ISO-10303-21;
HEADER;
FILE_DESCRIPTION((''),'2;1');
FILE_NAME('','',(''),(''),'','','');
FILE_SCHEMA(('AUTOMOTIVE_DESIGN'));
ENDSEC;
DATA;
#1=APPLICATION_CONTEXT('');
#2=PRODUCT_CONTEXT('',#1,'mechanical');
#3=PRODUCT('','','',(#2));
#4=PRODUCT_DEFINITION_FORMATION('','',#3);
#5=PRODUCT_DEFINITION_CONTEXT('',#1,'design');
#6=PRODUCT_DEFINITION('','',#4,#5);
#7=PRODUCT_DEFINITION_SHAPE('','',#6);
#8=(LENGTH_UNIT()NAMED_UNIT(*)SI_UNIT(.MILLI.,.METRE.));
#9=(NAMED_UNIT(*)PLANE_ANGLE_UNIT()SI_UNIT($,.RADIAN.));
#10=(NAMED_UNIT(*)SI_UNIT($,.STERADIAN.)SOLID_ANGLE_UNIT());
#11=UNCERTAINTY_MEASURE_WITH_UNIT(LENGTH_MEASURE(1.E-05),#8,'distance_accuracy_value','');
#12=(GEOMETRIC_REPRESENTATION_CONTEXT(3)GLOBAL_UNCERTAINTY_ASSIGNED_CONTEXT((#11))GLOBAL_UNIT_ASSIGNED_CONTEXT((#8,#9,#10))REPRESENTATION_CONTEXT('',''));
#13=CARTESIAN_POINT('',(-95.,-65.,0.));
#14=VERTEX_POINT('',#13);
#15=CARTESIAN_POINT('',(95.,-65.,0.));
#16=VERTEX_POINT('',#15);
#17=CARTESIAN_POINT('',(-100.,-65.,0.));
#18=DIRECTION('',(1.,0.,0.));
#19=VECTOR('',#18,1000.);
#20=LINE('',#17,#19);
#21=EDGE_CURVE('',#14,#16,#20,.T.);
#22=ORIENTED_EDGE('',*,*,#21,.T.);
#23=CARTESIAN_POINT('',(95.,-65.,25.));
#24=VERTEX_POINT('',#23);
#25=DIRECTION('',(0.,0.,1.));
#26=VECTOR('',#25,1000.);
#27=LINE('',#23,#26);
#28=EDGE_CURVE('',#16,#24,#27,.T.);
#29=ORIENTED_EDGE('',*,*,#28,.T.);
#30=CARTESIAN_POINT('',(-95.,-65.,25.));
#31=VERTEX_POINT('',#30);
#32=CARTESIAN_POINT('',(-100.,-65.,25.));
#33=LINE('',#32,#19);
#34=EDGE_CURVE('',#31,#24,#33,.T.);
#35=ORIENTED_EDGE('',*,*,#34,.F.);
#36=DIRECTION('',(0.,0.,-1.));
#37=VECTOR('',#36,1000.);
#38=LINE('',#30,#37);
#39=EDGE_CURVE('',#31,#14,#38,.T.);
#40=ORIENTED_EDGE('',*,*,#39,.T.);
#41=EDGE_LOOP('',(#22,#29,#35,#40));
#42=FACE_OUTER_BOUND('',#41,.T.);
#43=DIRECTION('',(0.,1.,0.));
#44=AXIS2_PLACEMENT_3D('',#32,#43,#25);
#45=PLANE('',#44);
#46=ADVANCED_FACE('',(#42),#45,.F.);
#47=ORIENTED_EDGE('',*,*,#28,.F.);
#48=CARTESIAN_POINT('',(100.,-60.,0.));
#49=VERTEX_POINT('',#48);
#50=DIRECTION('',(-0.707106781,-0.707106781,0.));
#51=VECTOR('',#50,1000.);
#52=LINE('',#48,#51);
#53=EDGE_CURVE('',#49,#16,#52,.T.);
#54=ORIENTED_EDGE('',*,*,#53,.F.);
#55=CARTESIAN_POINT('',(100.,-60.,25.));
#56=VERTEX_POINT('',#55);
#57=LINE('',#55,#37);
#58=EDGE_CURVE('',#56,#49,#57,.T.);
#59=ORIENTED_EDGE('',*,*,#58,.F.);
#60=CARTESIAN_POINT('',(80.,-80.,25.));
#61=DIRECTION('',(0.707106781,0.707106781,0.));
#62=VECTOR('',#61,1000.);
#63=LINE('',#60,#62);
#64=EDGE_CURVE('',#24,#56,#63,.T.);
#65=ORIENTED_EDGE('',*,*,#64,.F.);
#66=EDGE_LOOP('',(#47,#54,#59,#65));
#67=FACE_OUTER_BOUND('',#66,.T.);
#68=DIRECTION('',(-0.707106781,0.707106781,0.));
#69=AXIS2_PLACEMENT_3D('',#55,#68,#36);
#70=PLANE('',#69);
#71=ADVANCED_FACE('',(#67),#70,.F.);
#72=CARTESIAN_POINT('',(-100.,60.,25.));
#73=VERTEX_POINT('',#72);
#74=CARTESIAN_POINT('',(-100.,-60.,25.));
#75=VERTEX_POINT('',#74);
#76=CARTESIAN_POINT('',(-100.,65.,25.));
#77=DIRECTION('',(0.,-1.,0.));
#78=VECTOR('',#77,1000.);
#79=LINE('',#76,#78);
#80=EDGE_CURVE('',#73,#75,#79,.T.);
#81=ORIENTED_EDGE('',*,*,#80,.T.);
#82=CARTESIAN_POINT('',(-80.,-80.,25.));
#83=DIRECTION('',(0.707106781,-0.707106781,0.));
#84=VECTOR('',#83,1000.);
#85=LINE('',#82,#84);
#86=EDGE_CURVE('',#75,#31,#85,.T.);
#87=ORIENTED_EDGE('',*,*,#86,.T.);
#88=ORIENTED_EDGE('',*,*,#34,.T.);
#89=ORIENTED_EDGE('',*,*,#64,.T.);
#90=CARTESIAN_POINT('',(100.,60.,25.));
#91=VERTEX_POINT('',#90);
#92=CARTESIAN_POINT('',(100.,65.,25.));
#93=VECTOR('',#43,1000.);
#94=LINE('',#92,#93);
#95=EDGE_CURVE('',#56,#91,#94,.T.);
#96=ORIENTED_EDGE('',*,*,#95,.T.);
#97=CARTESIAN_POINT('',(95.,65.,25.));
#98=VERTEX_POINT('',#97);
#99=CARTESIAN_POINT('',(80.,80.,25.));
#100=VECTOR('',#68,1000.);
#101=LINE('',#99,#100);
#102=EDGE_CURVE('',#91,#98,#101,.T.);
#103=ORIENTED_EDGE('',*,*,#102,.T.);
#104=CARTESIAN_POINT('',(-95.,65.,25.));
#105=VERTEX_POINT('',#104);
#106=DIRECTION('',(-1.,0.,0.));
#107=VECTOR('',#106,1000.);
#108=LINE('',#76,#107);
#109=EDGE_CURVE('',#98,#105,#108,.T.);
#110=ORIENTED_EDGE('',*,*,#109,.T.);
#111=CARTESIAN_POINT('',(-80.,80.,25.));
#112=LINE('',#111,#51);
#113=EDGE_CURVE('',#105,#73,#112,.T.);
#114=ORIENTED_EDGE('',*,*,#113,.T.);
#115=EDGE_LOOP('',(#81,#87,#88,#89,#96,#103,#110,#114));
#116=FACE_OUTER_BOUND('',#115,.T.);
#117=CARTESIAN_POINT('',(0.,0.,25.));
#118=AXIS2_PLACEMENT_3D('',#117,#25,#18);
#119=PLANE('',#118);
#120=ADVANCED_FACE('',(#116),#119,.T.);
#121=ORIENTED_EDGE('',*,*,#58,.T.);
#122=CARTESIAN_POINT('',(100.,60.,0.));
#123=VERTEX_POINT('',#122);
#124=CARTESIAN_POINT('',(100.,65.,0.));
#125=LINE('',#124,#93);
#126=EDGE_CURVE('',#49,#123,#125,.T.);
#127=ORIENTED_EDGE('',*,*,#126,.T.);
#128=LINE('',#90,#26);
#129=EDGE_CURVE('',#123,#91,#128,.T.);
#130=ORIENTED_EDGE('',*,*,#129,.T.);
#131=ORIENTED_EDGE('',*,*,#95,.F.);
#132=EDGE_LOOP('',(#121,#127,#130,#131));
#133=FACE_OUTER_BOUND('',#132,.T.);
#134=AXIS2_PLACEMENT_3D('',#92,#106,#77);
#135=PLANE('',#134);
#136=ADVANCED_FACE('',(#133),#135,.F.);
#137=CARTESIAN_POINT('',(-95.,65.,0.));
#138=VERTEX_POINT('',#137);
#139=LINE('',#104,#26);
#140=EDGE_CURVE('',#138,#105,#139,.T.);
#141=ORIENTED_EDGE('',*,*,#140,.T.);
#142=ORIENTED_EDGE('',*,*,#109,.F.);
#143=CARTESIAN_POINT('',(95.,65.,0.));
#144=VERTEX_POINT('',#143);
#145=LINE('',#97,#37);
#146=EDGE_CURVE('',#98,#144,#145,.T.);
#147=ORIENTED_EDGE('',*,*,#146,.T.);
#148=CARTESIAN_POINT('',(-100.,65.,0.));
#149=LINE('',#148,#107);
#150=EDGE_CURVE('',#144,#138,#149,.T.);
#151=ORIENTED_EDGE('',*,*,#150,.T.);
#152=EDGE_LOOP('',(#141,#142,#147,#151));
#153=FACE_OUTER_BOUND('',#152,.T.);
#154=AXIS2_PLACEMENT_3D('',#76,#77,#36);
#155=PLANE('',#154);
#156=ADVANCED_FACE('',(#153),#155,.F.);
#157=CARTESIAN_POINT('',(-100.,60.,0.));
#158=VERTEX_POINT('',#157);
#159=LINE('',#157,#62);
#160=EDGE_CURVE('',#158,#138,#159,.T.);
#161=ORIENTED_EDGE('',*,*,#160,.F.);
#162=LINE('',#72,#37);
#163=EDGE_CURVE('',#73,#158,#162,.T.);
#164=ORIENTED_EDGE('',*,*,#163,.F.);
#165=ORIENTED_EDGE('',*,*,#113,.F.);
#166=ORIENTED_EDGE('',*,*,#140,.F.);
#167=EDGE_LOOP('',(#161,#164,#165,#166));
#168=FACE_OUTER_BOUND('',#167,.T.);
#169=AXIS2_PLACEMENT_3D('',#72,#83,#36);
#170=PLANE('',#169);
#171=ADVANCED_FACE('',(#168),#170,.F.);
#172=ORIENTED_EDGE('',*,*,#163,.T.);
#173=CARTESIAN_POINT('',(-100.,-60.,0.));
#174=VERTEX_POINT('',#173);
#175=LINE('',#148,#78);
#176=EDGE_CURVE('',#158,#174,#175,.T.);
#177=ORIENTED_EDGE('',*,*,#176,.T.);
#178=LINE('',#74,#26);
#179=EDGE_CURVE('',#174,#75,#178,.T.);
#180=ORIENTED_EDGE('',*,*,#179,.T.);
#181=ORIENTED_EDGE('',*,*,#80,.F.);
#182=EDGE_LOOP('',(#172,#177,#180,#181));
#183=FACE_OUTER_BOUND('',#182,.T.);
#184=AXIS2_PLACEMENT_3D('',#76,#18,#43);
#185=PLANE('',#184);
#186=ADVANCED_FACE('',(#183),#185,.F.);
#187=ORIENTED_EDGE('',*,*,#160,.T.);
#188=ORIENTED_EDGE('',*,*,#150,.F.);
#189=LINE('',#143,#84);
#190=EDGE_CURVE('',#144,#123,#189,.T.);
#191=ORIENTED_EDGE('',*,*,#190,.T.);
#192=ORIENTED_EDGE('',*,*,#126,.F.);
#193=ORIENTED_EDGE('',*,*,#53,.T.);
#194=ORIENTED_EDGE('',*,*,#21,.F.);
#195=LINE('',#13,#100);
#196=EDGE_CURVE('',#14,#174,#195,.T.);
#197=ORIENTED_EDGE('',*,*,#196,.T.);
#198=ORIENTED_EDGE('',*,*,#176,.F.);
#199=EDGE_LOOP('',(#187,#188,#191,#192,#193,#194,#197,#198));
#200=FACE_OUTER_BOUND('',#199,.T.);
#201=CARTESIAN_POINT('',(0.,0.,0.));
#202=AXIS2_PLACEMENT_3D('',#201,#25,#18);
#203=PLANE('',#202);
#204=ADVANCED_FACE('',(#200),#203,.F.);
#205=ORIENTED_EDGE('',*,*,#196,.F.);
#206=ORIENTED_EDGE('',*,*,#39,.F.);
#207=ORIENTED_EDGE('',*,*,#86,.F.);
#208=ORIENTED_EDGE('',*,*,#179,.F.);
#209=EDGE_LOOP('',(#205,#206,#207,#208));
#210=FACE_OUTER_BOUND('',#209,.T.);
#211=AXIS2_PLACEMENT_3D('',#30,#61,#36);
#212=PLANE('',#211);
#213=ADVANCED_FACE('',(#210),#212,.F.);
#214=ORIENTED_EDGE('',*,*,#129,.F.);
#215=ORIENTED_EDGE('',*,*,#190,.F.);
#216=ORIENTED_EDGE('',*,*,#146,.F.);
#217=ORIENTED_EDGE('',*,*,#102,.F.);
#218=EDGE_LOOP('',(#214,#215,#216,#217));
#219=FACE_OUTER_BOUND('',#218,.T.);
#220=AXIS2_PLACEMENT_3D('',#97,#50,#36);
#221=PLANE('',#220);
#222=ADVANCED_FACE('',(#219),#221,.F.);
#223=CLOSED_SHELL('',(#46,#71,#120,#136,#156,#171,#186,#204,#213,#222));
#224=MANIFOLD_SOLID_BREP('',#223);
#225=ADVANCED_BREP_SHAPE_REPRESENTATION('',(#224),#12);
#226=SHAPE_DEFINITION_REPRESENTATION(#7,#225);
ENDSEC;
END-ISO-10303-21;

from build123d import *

# Parameters (mm, degrees)
SKETCH_1_W      = 200
SKETCH_1_H      = 130
EXTRUDE_1_DEPTH = 25
CHAMFER_1_SIZE  = 5


with BuildPart() as part:
    # 草图1 → 凸台-拉伸1 (new body)
    with BuildSketch(Plane.XY):
        Rectangle(SKETCH_1_W, SKETCH_1_H)
    extrude(amount=EXTRUDE_1_DEPTH)

    # 倒角1
    chamfer_1_edges = [part.edges().sort_by_distance(p)[0] for p in [
        (100, -65, 12.5),
        (-100, -65, 12.5),
        (-100, 65, 12.5),
        (100, 65, 12.5),
    ]]
    chamfer(chamfer_1_edges, length=CHAMFER_1_SIZE)


solid = part.part
